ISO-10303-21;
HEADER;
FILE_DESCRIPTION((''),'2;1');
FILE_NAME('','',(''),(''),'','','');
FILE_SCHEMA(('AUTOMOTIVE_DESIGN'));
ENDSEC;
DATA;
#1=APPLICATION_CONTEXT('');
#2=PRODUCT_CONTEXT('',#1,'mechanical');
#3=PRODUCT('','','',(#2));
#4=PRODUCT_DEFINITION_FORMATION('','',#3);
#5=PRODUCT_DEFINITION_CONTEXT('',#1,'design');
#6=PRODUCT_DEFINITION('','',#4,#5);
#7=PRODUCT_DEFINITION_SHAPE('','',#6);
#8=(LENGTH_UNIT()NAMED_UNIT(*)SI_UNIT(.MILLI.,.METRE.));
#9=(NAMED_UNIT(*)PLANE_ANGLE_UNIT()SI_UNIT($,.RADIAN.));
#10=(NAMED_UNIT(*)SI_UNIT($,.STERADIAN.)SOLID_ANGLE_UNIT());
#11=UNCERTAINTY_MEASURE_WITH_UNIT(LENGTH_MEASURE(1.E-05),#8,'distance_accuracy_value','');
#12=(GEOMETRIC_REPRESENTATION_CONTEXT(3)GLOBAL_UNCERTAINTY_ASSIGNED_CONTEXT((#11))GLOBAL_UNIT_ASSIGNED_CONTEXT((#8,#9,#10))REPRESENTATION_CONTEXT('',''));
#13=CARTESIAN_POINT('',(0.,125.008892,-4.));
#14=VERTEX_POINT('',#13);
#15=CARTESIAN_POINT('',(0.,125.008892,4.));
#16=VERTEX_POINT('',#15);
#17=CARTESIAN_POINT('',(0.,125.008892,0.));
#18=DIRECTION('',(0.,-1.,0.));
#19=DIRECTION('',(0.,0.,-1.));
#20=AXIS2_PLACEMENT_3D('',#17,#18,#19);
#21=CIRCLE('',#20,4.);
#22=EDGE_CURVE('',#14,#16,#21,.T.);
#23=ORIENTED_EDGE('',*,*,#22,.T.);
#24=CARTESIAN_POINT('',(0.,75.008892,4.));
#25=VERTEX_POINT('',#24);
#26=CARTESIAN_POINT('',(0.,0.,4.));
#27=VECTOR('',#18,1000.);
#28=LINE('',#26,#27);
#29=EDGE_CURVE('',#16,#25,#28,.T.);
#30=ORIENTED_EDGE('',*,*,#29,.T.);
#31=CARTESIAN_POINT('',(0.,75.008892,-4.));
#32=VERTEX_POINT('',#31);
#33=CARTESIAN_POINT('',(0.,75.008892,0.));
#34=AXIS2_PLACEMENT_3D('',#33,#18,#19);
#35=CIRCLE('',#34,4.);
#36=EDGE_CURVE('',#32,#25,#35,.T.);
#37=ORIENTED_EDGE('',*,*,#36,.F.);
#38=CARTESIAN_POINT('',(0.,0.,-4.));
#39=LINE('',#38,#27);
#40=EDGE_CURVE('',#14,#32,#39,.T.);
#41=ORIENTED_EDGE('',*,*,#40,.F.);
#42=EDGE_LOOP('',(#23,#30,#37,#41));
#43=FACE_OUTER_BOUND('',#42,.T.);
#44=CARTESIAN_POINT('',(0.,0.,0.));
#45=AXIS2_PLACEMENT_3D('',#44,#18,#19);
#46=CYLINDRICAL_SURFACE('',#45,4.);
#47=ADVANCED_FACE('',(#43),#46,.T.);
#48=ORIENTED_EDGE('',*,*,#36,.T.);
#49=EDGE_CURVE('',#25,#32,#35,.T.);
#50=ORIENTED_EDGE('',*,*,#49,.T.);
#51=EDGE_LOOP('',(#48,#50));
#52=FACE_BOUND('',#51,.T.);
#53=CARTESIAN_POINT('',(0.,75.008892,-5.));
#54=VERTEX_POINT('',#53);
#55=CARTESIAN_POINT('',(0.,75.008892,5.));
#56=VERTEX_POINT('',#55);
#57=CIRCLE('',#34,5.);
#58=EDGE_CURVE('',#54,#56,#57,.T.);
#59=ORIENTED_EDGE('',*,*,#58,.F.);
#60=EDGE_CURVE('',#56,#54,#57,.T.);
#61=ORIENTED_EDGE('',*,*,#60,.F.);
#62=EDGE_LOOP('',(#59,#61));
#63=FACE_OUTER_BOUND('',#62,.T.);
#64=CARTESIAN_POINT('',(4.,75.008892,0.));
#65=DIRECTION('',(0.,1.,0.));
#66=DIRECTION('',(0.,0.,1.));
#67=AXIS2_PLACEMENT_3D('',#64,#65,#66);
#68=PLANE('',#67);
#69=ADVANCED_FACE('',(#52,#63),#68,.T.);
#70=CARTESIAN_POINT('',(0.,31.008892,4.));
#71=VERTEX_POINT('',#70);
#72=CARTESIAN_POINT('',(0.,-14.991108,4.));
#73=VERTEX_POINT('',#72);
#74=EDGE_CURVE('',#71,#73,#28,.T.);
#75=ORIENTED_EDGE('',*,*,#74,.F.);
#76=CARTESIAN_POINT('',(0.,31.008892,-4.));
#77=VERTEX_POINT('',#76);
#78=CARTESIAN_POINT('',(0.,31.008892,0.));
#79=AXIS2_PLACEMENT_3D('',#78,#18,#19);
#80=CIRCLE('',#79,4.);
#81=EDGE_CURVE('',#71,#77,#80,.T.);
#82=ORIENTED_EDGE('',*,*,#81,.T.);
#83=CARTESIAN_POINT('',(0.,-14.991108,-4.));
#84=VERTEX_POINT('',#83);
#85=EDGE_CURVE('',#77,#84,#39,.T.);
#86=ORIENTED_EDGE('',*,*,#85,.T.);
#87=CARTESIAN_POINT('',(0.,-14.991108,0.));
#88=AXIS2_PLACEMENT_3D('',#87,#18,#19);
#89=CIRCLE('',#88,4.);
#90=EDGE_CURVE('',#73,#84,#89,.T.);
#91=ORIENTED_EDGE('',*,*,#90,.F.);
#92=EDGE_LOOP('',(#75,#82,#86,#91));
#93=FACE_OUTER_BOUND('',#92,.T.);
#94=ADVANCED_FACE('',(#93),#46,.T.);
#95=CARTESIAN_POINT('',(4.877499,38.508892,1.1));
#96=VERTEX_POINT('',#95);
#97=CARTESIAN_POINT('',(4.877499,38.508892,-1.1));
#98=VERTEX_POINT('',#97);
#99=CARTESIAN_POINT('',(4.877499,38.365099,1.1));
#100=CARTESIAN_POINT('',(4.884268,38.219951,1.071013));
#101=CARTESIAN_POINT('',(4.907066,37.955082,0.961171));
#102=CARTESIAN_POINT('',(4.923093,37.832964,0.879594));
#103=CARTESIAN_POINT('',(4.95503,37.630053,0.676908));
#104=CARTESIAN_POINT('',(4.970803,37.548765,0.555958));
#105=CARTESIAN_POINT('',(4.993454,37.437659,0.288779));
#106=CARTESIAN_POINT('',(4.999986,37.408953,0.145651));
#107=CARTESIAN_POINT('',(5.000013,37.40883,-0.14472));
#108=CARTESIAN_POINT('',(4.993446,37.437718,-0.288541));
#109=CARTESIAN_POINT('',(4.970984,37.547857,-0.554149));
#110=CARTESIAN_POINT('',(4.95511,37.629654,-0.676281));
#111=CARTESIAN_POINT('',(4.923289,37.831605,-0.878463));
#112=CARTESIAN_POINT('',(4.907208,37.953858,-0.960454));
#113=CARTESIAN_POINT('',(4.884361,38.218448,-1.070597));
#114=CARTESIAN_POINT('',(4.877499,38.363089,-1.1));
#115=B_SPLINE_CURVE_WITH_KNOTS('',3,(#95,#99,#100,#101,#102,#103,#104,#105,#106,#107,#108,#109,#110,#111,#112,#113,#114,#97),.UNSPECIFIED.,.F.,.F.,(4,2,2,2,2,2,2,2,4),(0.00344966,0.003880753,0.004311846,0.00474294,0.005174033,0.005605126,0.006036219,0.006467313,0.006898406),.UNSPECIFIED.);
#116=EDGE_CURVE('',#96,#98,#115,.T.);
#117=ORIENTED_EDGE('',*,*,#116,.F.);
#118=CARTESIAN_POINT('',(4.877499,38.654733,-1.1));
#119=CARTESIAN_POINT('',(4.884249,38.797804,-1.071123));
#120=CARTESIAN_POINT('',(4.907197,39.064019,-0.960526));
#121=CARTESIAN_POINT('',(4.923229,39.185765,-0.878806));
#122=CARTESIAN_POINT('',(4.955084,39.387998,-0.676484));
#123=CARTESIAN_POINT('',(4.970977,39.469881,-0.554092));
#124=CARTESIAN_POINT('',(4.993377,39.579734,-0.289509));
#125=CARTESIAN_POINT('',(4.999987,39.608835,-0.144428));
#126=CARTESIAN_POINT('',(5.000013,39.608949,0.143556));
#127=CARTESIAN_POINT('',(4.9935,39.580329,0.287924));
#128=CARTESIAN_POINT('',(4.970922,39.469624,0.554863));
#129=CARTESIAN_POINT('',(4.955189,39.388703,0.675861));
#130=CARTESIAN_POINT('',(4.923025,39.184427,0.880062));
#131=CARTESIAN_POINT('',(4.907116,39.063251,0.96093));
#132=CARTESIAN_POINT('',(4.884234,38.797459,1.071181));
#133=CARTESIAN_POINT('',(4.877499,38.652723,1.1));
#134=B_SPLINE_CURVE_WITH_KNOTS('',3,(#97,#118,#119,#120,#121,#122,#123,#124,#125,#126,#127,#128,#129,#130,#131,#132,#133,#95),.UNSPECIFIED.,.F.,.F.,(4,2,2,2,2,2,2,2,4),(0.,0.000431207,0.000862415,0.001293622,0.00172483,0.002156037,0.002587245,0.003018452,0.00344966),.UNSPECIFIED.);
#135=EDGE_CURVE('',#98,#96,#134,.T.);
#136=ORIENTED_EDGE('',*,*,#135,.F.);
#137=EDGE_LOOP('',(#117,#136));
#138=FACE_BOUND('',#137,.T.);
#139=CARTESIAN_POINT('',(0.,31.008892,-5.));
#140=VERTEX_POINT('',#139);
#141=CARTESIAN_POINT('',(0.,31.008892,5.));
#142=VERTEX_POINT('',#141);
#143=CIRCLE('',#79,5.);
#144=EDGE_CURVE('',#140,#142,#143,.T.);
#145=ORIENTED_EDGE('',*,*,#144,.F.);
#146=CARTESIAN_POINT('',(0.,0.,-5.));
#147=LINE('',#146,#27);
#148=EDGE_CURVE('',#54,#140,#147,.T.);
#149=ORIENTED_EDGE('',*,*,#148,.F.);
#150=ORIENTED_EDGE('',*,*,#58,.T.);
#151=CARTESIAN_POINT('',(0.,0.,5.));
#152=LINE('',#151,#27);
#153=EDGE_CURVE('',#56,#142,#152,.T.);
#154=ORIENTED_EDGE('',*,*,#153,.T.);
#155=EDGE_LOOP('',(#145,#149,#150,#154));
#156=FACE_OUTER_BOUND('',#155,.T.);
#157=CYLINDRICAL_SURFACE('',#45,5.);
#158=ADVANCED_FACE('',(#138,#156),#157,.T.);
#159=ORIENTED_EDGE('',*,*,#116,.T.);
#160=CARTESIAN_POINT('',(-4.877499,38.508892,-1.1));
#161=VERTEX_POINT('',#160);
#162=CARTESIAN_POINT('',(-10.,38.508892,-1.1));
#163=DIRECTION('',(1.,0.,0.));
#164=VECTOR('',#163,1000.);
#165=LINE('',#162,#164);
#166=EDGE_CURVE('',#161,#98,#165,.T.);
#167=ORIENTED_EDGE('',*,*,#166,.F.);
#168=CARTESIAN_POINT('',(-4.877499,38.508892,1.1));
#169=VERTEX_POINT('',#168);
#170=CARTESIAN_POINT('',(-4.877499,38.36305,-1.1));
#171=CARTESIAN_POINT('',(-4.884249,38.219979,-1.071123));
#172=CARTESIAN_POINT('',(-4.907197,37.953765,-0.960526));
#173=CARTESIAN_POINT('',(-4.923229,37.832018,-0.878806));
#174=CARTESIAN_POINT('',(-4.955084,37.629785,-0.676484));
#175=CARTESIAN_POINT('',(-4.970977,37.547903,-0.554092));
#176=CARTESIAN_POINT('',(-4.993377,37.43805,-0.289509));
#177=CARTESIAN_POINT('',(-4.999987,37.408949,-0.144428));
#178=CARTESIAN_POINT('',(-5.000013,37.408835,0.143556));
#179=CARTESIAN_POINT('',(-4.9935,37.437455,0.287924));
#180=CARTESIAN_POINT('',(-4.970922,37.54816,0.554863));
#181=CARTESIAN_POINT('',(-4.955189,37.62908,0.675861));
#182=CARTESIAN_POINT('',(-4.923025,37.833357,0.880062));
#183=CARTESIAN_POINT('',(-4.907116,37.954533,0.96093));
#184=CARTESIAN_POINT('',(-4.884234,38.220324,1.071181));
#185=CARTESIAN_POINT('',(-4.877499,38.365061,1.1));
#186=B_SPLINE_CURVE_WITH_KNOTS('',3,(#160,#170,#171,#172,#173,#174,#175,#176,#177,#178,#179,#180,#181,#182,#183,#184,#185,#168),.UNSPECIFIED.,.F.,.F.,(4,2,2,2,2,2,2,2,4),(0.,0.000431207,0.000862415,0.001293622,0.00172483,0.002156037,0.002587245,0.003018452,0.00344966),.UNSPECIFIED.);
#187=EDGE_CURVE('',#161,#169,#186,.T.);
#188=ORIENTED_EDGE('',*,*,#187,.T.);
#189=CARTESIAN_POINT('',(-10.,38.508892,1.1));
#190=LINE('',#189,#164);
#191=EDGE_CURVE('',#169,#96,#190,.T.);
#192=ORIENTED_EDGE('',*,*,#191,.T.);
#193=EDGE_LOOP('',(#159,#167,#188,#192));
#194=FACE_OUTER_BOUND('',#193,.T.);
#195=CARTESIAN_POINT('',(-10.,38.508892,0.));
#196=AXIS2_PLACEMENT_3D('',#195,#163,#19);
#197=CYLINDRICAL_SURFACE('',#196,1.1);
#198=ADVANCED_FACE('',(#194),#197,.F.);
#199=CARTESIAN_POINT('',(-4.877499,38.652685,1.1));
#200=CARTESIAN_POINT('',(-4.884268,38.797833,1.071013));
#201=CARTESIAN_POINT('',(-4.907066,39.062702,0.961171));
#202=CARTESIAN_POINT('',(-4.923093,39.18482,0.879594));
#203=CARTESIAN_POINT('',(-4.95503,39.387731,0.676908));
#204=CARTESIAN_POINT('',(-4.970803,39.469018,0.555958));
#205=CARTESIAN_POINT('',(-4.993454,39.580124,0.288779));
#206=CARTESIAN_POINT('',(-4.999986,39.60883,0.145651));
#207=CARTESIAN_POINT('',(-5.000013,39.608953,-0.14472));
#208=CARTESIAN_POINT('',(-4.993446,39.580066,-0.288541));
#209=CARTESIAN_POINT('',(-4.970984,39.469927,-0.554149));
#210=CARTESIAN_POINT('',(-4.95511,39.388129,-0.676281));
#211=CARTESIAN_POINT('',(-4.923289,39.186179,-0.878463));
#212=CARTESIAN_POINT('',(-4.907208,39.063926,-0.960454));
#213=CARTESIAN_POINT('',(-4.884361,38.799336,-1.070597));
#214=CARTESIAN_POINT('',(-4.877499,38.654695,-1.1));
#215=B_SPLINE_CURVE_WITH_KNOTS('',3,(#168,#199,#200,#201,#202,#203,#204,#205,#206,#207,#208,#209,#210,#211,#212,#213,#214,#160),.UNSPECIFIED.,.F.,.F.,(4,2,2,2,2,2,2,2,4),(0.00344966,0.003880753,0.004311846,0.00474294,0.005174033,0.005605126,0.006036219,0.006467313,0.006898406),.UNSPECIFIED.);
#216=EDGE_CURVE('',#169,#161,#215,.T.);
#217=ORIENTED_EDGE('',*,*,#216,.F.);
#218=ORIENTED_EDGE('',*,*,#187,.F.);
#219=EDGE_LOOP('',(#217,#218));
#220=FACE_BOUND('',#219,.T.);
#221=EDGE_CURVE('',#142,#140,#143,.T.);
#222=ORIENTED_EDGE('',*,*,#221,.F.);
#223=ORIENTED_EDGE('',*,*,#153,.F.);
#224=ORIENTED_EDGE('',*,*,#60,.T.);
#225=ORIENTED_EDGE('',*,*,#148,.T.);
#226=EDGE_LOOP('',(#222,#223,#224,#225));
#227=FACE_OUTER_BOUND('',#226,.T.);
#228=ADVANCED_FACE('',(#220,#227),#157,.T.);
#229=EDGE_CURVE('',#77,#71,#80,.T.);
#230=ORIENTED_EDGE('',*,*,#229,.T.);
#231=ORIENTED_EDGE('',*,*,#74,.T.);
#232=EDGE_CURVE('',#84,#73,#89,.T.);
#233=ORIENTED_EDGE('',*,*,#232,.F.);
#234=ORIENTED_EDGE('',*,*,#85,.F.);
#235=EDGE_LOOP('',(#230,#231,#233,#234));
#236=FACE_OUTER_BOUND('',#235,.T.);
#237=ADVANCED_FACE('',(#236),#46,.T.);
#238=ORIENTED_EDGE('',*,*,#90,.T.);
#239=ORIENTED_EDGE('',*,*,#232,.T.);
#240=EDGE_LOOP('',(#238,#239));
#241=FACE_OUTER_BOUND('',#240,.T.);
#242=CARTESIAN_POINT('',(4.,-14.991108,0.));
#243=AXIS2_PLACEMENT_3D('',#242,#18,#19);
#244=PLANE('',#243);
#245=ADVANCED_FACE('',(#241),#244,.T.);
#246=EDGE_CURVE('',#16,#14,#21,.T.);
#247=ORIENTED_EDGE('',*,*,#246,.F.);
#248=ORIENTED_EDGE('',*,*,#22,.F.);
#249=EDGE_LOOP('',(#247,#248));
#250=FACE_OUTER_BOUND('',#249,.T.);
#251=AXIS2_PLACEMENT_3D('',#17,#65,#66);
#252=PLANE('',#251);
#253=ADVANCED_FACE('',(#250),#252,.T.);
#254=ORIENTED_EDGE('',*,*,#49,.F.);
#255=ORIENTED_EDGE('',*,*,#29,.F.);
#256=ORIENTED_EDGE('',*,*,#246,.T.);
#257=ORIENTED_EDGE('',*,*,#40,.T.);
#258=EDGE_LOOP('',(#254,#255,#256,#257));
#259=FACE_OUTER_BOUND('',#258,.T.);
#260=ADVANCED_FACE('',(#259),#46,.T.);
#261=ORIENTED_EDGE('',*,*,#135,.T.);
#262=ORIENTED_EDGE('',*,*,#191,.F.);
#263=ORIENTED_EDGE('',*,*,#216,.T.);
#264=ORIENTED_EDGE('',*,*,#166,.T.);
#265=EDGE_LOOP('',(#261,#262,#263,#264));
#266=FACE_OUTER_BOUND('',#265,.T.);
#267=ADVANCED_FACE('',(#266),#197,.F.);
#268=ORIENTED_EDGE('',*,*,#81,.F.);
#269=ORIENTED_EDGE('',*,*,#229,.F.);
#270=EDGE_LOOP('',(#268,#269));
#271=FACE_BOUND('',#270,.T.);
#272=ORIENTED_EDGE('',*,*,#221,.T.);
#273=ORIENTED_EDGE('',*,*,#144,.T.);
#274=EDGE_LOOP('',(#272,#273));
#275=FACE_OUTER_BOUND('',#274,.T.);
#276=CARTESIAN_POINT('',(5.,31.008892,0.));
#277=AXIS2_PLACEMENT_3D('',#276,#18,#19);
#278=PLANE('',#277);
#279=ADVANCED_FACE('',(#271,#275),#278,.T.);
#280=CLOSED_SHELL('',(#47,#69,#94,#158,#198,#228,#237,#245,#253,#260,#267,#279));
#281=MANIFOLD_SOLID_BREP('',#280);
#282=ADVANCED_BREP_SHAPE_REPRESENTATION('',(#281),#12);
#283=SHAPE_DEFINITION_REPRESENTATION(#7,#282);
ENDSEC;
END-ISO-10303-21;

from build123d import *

# Parameters (mm, degrees)
SKETCH_5_R          = 1.1
CUT_EXTRUDE_1_DEPTH = 10


with BuildPart() as part:
    # 草图4 → 旋转1 (revolve)
    with BuildSketch(Plane.XY, mode=Mode.PRIVATE) as revolve_1_sk:
        Polygon((0, 125.008891803), (4, 125.008891803), (4, 75.008891803), (5, 75.008891803), (5, 31.008891803), (4, 31.008891803), (4, -14.991108197), (0, -14.991108197), align=None)
    revolve(revolve_1_sk.sketch.rotate(Axis((0, 0, 0), (0, 1, 0)), 90), axis=Axis((0, 0, 0), (0, 1, 0)))

    # 草图5 → 切除-拉伸1 (cut, symmetric)
    with BuildSketch(Plane(origin=(0, 0, 0), x_dir=(0, 0, -1), z_dir=(1, 0, 0))):
        with Locations((0, 38.508891803)):
            Circle(SKETCH_5_R)
    extrude(amount=CUT_EXTRUDE_1_DEPTH, both=True, mode=Mode.SUBTRACT)


solid = part.part
